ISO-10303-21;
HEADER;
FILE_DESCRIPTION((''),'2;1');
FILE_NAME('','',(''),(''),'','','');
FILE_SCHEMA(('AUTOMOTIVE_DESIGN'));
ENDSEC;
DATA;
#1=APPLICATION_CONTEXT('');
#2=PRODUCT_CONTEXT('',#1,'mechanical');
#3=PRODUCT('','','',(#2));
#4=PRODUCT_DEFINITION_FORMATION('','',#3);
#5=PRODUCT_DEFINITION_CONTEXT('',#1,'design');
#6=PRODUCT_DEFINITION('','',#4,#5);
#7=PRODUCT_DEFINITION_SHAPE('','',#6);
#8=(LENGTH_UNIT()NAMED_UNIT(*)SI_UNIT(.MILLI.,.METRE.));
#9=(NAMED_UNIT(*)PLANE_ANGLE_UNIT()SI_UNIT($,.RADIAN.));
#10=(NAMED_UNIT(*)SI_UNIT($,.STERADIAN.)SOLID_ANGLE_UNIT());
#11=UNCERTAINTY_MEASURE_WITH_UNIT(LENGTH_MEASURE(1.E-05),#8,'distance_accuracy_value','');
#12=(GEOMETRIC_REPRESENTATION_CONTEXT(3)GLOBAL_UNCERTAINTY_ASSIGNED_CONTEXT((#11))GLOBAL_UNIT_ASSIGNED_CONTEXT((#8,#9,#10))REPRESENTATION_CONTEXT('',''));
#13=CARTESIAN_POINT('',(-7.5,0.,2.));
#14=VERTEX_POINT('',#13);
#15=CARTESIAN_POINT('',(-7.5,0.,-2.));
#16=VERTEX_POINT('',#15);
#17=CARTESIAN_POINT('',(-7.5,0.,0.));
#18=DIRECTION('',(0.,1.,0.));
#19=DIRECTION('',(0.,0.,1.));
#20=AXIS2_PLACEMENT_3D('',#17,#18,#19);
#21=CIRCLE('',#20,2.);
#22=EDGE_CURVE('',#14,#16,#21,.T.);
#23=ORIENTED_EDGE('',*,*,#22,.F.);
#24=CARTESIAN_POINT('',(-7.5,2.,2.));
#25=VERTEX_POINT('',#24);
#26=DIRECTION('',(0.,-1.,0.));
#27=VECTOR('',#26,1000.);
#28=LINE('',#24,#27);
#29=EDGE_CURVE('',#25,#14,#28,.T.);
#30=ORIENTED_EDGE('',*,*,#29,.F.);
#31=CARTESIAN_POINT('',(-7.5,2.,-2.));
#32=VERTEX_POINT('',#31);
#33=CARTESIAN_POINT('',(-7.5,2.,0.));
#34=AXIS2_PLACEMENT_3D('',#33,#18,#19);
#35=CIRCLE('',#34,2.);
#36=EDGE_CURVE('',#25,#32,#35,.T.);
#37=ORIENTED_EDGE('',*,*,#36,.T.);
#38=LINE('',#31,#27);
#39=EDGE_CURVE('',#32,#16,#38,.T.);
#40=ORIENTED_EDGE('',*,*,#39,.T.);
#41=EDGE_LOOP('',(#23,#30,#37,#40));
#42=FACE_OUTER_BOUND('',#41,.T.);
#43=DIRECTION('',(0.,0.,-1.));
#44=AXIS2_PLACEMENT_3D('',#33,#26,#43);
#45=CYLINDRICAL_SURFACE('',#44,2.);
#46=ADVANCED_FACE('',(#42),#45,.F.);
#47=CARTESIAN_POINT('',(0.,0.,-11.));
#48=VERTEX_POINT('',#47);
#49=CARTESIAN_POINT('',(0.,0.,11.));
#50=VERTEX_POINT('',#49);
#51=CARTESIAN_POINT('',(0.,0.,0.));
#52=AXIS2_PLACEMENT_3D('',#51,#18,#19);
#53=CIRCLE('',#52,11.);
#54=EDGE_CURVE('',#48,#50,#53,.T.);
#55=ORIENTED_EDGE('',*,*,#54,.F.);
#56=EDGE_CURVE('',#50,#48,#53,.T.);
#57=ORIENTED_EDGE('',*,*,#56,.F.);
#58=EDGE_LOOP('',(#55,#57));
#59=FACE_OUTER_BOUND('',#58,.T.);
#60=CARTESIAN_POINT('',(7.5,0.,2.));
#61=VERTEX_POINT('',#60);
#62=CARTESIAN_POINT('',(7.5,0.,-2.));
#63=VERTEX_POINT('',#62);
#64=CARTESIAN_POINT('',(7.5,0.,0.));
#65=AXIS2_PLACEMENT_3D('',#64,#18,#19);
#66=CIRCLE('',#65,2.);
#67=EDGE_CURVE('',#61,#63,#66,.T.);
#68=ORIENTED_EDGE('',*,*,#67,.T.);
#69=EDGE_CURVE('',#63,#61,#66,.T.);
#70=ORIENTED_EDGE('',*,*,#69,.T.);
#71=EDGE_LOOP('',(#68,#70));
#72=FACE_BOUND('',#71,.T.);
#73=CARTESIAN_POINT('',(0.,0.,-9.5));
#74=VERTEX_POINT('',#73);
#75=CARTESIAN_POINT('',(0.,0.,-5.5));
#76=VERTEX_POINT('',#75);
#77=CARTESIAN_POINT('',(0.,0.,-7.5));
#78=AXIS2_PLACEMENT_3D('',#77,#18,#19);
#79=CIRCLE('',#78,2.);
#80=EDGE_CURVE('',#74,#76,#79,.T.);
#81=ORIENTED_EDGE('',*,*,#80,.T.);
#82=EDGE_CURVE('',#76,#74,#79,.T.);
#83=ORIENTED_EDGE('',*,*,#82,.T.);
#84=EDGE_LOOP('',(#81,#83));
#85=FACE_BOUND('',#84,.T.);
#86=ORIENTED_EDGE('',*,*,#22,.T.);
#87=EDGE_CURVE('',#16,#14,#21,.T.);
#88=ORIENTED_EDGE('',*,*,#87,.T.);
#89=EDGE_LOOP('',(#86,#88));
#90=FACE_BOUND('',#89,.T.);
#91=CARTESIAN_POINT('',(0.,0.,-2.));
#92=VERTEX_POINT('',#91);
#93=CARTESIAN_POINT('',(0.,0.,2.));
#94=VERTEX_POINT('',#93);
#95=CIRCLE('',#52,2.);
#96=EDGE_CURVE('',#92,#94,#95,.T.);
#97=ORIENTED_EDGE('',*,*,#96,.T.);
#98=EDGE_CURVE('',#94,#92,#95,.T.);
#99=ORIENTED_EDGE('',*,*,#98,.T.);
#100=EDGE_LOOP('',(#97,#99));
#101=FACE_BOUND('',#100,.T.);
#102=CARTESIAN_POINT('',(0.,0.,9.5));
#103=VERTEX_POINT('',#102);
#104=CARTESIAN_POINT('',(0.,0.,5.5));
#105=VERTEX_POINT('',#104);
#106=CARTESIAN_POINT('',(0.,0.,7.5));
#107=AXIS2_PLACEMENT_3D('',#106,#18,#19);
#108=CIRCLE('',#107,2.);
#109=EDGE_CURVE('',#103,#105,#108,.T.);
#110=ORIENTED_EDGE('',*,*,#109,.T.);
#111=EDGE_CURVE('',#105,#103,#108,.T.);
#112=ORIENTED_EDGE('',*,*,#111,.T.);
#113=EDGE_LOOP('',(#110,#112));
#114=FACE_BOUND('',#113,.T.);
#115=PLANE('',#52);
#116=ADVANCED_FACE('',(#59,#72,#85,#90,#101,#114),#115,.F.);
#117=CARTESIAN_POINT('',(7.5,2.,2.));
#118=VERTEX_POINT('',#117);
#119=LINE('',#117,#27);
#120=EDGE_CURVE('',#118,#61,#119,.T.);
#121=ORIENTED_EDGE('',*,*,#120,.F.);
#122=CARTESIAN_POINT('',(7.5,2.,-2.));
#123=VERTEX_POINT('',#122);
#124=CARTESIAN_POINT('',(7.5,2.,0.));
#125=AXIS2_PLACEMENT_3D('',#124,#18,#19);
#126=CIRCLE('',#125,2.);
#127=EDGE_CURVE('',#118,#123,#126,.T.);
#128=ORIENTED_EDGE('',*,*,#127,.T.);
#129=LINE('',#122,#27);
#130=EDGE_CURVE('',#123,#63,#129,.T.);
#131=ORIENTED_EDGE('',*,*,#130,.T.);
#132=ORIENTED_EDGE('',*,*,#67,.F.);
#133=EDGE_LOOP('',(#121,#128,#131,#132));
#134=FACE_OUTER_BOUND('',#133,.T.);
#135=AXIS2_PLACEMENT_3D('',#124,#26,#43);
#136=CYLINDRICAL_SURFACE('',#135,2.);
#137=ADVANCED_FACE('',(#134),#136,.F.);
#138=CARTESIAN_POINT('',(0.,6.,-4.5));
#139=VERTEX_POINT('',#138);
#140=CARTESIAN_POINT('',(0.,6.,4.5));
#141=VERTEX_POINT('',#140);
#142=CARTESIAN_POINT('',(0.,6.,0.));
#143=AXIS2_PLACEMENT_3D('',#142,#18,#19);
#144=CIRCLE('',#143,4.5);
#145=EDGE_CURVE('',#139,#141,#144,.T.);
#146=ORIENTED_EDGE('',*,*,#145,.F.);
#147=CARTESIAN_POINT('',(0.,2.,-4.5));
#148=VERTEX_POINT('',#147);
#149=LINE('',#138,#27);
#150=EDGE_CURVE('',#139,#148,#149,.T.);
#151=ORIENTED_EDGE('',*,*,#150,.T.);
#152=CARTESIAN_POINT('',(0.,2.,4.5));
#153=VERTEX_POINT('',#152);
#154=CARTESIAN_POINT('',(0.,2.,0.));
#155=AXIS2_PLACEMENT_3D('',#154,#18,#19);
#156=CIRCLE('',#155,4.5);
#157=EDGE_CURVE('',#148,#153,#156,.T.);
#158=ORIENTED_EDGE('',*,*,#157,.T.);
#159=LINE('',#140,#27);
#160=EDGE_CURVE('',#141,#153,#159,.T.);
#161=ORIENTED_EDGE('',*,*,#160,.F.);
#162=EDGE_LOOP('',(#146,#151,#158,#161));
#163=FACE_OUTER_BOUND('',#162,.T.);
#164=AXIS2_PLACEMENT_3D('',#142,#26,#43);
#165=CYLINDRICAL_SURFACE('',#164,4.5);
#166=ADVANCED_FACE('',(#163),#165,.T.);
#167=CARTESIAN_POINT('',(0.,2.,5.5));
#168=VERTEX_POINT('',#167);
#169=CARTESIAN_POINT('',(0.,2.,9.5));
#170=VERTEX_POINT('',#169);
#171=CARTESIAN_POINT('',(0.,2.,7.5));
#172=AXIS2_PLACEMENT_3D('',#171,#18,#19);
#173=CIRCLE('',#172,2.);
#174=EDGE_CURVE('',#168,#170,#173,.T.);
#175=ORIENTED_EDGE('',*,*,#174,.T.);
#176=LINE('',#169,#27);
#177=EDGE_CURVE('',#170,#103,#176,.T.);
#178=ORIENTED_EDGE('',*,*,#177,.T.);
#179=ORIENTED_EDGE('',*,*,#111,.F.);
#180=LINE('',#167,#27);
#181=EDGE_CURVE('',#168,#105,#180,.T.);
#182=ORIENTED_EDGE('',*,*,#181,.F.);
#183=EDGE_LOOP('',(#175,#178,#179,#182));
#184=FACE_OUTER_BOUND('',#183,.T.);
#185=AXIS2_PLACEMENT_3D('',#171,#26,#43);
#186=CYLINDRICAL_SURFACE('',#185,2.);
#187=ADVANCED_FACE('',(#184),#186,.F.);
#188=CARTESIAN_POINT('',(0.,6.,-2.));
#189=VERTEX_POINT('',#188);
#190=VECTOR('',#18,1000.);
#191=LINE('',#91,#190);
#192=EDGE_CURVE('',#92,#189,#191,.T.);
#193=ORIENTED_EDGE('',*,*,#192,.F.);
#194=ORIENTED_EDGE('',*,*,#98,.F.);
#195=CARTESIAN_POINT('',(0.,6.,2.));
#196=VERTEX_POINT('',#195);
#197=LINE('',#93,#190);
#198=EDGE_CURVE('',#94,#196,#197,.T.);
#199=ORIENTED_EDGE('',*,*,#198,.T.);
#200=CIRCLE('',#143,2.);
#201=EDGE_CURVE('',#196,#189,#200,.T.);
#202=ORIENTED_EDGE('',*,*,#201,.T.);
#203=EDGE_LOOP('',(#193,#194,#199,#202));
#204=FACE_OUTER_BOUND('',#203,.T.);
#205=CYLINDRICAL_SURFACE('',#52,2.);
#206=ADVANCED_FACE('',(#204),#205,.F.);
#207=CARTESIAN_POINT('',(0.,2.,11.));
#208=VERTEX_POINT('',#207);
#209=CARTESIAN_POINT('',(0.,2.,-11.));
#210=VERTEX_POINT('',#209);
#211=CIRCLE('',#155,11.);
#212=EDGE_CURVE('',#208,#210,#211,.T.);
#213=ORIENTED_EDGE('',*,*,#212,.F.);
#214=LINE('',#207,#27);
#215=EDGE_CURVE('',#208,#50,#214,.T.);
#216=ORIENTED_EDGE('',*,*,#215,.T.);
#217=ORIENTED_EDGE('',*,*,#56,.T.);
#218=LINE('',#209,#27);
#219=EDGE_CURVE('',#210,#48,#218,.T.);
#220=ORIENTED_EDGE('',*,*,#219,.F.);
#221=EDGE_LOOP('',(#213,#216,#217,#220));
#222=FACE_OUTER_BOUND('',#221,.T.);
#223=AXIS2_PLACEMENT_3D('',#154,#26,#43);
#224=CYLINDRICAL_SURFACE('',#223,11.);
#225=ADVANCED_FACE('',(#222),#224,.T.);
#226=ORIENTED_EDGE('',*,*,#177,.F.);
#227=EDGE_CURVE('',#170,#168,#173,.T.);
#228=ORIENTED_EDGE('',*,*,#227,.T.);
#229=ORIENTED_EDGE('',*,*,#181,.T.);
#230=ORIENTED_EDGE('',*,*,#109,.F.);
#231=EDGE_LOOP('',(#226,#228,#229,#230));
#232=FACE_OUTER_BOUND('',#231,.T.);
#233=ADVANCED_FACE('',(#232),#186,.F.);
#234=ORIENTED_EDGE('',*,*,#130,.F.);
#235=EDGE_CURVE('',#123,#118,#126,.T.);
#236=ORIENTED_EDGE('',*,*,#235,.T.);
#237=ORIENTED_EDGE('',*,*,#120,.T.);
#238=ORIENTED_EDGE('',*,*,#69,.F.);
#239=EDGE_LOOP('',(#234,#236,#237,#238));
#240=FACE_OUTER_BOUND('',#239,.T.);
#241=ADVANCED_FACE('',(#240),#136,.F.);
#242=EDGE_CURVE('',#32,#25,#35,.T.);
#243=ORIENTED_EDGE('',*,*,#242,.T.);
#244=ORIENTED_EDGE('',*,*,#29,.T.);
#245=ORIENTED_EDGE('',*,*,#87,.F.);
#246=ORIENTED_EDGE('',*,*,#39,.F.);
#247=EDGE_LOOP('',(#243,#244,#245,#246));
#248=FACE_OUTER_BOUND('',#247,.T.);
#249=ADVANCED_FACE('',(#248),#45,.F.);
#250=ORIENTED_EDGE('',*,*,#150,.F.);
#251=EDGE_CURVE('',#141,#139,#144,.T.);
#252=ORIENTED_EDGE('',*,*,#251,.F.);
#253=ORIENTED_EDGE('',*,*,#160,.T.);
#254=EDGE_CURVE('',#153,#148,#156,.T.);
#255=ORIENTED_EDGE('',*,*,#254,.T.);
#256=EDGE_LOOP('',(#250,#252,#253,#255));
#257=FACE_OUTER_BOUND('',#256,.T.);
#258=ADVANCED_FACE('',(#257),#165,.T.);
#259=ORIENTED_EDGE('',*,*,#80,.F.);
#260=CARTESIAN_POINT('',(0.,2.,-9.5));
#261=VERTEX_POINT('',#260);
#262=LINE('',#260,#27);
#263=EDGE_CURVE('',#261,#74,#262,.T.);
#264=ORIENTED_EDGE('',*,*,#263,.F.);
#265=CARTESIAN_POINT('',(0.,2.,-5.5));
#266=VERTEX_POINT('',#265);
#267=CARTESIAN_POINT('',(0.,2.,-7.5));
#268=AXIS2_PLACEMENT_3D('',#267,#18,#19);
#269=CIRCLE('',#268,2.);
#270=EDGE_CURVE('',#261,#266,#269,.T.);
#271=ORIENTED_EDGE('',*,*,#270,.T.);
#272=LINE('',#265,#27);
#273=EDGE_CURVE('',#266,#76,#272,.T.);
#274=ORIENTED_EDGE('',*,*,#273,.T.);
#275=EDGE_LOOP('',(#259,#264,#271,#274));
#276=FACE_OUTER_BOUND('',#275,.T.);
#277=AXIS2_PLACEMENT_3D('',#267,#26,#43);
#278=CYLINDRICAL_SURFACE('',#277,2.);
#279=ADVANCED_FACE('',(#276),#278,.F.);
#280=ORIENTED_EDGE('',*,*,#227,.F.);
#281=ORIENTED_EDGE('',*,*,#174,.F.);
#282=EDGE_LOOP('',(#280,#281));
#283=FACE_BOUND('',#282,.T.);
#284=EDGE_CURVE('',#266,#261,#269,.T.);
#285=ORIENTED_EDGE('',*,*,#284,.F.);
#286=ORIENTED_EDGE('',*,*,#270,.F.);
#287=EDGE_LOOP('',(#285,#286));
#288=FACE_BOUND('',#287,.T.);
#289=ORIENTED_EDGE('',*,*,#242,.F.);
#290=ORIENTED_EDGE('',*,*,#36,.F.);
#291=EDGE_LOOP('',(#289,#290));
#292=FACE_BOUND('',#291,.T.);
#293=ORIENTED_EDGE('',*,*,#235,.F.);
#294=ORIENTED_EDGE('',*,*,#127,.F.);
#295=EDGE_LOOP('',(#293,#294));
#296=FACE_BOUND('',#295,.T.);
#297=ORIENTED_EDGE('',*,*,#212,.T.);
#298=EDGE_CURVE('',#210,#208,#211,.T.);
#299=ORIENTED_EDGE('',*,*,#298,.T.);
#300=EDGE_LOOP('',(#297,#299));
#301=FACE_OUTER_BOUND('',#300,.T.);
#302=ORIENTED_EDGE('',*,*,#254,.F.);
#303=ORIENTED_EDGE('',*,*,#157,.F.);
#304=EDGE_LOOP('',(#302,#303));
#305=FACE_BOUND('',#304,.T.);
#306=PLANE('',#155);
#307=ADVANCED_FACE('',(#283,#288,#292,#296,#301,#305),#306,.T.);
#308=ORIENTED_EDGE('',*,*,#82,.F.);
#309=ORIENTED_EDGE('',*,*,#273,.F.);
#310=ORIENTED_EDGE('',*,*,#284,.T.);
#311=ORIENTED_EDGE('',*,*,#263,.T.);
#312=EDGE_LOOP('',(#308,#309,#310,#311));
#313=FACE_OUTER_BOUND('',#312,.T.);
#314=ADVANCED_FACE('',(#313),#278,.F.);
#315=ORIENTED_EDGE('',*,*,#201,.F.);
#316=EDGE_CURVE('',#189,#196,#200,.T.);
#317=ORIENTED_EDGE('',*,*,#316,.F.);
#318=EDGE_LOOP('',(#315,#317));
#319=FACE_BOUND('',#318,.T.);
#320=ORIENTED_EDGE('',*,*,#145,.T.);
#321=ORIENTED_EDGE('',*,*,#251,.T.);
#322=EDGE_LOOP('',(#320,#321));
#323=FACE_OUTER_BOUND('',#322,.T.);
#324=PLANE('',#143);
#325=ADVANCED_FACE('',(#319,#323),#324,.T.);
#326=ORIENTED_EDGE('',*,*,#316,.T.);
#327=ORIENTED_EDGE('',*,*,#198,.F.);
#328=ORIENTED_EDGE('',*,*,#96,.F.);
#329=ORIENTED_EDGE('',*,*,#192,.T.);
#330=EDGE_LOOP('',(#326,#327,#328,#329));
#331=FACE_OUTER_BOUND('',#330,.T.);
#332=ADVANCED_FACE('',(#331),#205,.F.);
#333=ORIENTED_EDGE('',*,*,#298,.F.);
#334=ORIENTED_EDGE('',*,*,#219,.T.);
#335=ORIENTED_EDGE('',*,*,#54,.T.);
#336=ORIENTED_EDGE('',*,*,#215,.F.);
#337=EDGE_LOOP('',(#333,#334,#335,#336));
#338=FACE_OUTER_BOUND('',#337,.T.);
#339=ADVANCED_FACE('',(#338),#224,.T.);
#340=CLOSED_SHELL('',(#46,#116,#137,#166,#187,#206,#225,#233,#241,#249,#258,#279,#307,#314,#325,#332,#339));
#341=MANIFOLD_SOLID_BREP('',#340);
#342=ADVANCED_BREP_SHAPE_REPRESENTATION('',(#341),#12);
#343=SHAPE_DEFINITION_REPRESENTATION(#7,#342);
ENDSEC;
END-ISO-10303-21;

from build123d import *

# Parameters (mm, degrees)
SKETCH1_R               = 11
SKETCH1_R_2             = 2
BOSS_EXTRUDE1_DEPTH     = 2
SKETCH2_R               = 4.5
BOSS_EXTRUDE2_DEPTH     = 4
CUT_EXTRUDE1_DEPTH      = 17.673332001
CUT_EXTRUDE1_DEPTH_BACK = 17.673332001
SKETCH3_R               = 2


with BuildPart() as part:
    # Sketch1 → Boss-Extrude1 (new body)
    with BuildSketch(Plane(origin=(0, 0, 0), x_dir=(1, 0, 0), z_dir=(0, 1, 0))):
        with Locations(Location((0, 0, 0), (0, 0, 270))):
            Circle(SKETCH1_R)
        with Locations(Location((0, 7.5, 0), (0, 0, 270))):
            Circle(SKETCH1_R_2, mode=Mode.SUBTRACT)
        with Locations(Location((7.5, 0, 0), (0, 0, 270))):
            Circle(SKETCH1_R_2, mode=Mode.SUBTRACT)
        with Locations(Location((0, -7.5, 0), (0, 0, 270))):
            Circle(SKETCH1_R_2, mode=Mode.SUBTRACT)
        with Locations(Location((-7.5, 0, 0), (0, 0, 270))):
            Circle(SKETCH1_R_2, mode=Mode.SUBTRACT)
    extrude(amount=BOSS_EXTRUDE1_DEPTH)

    # Sketch2 → Boss-Extrude2 (add)
    with BuildSketch(Plane(origin=(0, 2, 0), x_dir=(1, 0, 0), z_dir=(0, 1, 0))):
        with Locations(Location((0, 0, 0), (0, 0, 270))):
            Circle(SKETCH2_R)
    extrude(amount=BOSS_EXTRUDE2_DEPTH)

    # Sketch3 → Cut-Extrude1 (cut, two sides: drawn at the far end of the back side and taken through both)
    with BuildSketch(Plane(origin=(0, 6, 0), x_dir=(1, 0, 0), z_dir=(0, 1, 0)).offset(-CUT_EXTRUDE1_DEPTH_BACK)):
        with Locations(Location((0, 0, 0), (0, 0, 270))):
            Circle(SKETCH3_R)
    extrude(amount=CUT_EXTRUDE1_DEPTH + CUT_EXTRUDE1_DEPTH_BACK, mode=Mode.SUBTRACT)


solid = part.part
